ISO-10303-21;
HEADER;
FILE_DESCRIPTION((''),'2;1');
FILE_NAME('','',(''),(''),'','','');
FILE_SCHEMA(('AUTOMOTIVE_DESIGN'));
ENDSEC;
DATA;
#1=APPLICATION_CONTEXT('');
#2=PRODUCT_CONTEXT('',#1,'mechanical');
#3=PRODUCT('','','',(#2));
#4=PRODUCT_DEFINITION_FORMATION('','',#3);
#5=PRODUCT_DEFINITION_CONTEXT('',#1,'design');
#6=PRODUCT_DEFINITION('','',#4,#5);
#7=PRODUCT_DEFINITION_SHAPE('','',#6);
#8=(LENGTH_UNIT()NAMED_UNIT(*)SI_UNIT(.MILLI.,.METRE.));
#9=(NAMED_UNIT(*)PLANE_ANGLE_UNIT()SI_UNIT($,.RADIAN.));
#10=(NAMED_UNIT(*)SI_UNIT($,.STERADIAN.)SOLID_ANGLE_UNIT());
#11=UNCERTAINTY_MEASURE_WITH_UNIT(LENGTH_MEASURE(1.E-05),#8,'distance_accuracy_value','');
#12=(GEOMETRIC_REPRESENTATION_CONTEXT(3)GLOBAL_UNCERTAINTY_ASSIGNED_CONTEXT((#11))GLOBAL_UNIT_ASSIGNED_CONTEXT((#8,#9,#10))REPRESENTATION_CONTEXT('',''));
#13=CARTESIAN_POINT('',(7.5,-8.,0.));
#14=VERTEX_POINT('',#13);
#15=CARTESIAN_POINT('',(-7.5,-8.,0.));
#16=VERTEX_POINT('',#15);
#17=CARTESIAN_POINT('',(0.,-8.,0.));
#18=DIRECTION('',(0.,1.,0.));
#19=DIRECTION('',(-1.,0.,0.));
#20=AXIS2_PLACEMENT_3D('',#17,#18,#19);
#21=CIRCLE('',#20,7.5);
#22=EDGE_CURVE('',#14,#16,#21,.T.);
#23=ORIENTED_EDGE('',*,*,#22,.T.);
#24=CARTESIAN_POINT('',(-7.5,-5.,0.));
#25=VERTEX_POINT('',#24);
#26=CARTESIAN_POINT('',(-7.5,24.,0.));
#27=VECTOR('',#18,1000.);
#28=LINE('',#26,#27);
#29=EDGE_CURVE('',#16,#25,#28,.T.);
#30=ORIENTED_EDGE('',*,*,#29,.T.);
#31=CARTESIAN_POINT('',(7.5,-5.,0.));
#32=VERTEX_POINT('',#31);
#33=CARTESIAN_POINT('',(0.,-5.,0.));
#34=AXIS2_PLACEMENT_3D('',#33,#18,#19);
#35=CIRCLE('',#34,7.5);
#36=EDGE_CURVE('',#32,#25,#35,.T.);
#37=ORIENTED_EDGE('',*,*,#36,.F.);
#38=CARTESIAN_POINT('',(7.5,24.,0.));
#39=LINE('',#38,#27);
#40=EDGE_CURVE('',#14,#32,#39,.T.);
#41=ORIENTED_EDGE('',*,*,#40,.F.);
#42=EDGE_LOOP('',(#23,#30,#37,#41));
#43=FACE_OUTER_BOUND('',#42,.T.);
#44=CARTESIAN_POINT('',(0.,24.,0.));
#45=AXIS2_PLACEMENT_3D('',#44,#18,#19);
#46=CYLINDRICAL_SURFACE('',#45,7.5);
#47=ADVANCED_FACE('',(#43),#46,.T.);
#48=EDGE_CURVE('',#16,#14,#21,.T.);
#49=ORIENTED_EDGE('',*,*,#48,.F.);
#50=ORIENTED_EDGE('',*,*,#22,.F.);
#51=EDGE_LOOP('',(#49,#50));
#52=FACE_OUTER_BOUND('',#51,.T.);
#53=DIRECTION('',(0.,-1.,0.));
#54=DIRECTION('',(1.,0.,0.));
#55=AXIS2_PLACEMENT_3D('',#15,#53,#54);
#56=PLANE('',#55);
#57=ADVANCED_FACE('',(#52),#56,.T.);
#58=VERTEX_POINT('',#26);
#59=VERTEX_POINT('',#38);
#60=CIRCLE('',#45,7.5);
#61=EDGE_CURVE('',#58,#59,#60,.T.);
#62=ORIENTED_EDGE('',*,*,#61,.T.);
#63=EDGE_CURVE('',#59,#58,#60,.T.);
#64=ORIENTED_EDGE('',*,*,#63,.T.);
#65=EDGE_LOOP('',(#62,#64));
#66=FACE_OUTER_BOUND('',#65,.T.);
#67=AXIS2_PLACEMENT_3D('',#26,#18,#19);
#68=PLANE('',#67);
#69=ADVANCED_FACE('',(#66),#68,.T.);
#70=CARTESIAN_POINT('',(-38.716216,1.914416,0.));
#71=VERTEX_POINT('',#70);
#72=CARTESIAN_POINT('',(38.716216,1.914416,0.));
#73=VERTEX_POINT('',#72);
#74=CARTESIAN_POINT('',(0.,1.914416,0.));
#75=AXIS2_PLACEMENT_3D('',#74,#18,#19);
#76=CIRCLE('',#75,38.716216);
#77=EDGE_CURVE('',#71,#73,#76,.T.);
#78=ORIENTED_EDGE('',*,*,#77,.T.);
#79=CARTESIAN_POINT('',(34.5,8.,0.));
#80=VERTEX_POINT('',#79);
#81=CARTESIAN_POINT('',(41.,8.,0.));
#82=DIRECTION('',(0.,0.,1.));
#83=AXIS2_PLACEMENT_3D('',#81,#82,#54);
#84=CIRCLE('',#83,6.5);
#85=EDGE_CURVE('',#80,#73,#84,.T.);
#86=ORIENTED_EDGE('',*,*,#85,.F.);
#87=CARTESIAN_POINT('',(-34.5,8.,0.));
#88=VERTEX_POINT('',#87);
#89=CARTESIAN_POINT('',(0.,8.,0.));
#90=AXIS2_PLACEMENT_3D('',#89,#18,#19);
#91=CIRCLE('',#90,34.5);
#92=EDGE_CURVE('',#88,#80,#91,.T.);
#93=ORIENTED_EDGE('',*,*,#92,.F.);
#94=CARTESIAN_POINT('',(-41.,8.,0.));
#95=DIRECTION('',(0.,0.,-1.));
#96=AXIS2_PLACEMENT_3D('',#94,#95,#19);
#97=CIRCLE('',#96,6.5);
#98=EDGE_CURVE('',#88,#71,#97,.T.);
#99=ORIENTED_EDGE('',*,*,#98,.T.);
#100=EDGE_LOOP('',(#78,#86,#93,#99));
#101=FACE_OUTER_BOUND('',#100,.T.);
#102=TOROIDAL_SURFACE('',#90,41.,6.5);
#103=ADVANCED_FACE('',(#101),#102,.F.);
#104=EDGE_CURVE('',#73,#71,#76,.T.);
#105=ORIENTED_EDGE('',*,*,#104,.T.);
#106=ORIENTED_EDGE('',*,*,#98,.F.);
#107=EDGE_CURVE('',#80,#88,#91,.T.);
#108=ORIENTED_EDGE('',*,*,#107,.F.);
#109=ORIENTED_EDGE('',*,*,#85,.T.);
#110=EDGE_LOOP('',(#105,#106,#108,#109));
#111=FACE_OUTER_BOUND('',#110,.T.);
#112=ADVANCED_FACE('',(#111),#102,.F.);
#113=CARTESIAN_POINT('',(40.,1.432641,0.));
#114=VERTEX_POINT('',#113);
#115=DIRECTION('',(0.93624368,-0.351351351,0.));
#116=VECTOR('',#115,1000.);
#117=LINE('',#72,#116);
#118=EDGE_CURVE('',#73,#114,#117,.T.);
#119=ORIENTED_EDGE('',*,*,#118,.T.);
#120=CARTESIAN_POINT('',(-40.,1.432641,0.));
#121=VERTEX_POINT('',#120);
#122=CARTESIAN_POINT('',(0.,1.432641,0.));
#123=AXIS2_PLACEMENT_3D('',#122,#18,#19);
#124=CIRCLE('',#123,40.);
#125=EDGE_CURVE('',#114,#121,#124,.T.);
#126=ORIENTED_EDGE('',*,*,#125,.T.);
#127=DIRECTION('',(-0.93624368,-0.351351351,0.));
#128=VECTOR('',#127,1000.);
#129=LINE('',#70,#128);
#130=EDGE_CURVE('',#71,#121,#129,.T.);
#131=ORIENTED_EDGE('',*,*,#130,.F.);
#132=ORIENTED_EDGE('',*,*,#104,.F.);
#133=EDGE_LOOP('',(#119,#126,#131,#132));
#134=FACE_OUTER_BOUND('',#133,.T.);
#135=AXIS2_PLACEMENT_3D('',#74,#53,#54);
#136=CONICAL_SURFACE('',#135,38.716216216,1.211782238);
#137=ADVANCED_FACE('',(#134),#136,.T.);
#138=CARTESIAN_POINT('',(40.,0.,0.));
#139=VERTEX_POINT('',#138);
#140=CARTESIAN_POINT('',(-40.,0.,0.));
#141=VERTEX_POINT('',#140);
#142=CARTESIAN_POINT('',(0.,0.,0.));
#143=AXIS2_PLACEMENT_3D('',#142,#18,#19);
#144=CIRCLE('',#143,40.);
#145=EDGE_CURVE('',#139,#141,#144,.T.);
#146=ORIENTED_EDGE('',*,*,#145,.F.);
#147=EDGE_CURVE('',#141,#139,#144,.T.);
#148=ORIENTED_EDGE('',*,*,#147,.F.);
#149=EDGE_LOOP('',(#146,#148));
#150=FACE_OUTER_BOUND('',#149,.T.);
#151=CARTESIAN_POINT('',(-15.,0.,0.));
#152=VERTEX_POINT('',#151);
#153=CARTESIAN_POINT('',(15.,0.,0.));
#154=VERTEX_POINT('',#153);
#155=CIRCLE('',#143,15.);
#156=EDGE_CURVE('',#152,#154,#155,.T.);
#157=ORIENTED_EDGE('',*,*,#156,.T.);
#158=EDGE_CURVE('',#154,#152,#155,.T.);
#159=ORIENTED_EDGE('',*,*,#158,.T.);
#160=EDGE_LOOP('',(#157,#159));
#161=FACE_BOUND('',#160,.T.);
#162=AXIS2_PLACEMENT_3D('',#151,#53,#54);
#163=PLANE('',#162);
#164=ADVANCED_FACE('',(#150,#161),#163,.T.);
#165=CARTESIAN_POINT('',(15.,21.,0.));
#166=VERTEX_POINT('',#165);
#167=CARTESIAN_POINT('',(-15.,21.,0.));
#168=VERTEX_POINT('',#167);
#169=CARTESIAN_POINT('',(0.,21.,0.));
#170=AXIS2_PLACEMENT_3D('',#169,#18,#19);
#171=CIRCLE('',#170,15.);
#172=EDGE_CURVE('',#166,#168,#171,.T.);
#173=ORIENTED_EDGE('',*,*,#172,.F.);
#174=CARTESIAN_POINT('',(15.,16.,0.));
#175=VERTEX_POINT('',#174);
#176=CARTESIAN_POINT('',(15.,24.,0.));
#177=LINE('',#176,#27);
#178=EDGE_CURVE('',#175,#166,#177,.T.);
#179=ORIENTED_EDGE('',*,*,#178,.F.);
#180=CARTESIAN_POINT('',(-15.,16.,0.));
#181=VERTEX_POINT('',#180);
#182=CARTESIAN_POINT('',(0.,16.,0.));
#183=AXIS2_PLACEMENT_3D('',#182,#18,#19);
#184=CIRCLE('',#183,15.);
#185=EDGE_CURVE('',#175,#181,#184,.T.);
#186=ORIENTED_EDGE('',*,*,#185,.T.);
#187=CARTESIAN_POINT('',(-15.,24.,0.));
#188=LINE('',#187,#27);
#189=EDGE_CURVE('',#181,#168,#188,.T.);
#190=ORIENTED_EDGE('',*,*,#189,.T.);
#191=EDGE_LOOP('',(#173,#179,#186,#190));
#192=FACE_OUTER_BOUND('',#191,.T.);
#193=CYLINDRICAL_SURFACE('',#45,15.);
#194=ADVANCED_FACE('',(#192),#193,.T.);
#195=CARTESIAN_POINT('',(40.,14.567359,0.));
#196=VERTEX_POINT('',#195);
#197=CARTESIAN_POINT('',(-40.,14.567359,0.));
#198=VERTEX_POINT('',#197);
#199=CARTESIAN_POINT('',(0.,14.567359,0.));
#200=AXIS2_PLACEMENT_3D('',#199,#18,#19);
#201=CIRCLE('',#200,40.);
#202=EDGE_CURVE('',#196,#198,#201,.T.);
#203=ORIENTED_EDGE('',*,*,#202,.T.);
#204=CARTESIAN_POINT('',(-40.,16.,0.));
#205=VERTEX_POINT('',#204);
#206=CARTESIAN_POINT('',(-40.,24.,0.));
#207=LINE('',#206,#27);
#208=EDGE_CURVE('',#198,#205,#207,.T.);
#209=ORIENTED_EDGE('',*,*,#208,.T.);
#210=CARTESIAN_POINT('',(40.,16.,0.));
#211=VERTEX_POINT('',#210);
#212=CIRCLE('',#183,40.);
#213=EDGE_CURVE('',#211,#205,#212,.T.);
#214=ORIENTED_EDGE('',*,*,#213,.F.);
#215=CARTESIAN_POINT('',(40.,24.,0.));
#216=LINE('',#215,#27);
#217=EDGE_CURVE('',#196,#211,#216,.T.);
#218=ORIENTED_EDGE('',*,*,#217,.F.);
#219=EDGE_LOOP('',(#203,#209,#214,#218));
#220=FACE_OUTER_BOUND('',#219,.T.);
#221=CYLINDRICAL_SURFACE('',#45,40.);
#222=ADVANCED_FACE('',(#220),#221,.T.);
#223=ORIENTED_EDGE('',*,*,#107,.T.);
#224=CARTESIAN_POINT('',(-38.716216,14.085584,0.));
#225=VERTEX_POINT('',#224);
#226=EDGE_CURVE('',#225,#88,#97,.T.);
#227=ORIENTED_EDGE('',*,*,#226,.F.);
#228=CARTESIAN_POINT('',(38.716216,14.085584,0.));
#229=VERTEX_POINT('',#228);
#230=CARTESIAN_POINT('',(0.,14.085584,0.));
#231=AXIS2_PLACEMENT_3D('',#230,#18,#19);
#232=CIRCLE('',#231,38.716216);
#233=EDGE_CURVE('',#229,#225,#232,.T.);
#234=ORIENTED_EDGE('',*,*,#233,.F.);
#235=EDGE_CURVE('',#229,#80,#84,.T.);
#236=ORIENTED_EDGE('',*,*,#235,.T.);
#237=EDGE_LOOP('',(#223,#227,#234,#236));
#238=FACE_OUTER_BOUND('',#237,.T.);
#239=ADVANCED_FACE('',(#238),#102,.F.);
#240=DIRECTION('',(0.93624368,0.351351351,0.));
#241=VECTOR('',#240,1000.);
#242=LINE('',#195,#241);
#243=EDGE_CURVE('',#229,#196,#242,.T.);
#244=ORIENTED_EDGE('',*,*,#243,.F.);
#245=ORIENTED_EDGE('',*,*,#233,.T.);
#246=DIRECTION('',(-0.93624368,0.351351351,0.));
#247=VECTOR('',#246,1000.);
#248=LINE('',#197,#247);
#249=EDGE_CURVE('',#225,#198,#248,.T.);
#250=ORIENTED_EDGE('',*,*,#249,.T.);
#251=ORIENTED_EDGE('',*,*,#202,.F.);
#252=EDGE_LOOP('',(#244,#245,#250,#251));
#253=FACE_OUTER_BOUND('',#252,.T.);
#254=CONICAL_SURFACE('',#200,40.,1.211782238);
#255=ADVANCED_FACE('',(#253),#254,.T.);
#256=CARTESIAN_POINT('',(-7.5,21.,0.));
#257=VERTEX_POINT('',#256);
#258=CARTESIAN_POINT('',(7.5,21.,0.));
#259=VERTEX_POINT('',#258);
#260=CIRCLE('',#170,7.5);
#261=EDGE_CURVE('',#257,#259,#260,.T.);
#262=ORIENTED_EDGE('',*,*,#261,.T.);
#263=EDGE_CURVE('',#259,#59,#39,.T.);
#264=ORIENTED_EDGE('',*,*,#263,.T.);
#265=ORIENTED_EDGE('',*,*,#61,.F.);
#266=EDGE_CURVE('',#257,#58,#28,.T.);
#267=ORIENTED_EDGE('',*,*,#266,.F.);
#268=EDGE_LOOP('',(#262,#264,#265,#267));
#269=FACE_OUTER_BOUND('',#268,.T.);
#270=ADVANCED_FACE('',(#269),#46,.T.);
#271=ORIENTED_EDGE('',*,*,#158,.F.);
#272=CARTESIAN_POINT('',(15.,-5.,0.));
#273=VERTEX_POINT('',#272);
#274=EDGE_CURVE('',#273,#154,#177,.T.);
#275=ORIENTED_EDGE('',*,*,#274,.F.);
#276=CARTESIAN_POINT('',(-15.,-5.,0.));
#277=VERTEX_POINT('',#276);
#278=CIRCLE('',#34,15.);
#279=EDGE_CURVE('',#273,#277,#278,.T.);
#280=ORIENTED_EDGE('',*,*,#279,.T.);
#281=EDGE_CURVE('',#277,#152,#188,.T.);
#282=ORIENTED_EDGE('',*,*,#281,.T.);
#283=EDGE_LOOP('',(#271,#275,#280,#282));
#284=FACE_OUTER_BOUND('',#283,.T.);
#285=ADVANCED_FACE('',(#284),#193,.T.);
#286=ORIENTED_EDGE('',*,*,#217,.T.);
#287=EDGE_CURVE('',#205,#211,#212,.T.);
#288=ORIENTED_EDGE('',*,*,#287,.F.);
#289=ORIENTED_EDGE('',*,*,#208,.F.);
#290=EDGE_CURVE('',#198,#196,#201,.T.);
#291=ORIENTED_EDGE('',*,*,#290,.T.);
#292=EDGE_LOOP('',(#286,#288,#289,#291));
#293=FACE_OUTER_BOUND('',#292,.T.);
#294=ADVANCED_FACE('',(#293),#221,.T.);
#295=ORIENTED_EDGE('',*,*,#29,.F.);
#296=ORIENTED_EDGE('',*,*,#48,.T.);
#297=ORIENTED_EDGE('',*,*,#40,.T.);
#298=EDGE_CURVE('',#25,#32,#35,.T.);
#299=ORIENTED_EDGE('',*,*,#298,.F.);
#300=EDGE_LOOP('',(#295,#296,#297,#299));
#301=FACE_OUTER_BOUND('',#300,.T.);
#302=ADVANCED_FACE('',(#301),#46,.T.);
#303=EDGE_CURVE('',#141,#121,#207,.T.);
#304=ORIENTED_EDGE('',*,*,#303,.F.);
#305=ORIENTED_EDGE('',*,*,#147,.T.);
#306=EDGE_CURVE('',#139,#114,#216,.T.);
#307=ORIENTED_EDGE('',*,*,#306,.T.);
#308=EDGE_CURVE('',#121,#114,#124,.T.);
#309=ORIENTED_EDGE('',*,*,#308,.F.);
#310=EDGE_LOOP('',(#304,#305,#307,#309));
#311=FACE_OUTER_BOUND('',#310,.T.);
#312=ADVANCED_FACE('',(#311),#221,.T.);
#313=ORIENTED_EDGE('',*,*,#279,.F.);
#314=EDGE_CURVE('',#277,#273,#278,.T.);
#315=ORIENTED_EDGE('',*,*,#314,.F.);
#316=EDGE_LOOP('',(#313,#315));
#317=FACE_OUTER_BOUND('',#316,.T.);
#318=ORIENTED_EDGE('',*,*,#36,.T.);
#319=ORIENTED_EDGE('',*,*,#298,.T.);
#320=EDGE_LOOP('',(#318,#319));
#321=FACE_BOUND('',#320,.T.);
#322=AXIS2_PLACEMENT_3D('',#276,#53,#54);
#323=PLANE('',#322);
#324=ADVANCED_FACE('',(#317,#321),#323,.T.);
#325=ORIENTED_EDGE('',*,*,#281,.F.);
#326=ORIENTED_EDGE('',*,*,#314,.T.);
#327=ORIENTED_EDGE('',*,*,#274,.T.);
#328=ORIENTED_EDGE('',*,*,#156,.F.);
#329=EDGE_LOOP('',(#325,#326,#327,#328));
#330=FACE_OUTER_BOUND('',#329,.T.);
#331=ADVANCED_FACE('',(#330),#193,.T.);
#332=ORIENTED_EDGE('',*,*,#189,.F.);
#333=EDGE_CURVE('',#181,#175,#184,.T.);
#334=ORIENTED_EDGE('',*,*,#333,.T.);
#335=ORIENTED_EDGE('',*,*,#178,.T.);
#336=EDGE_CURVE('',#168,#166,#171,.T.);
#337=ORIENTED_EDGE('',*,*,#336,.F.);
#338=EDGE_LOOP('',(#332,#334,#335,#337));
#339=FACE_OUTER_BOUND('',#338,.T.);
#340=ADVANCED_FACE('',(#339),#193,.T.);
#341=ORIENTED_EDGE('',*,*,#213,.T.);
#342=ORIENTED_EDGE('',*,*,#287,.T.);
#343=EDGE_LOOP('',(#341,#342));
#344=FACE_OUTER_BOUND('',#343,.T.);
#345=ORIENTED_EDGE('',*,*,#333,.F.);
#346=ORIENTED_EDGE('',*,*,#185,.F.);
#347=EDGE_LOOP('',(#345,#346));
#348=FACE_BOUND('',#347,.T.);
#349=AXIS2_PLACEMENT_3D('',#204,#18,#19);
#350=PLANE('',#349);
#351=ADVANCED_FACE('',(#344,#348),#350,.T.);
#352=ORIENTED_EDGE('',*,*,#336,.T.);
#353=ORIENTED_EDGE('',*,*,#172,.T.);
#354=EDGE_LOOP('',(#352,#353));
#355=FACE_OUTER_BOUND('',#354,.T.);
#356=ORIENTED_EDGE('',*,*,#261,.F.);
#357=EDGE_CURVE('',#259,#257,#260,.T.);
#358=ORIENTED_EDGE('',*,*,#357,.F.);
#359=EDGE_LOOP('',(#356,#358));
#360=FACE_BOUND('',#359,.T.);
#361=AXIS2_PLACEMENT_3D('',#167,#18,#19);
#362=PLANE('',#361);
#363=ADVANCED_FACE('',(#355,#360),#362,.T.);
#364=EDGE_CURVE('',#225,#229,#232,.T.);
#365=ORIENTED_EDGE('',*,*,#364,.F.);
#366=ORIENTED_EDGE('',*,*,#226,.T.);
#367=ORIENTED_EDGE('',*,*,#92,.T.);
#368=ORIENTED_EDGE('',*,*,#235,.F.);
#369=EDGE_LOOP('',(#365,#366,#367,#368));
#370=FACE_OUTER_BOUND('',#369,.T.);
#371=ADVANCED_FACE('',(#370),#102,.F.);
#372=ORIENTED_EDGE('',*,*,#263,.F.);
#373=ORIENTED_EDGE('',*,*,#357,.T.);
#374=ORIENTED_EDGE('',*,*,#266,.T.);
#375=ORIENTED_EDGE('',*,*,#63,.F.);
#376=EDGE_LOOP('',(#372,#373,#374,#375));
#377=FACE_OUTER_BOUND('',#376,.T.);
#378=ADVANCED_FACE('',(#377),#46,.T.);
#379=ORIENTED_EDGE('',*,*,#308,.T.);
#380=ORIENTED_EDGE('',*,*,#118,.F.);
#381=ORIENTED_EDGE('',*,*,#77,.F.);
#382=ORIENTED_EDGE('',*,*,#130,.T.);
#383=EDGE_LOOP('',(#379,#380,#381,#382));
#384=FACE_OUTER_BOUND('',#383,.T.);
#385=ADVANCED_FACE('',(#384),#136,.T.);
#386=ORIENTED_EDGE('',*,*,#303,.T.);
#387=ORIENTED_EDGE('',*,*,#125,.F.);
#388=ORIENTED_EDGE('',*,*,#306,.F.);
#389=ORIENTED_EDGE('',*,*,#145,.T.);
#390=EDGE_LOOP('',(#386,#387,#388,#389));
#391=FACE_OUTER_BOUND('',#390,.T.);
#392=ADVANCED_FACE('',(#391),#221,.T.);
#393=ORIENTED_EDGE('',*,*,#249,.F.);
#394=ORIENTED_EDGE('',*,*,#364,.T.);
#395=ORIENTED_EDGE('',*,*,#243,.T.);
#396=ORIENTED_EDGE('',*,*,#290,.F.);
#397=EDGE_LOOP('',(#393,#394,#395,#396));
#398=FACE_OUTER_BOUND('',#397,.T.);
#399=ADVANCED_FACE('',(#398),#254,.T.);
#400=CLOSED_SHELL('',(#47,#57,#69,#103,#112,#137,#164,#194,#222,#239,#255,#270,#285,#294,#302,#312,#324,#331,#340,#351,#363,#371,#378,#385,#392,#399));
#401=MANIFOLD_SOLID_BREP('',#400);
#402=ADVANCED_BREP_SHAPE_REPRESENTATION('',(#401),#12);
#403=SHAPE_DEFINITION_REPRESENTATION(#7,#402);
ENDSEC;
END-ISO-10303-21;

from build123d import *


with BuildPart() as part:
    # Sketch1 → Revolve1 (revolve)
    with BuildSketch(Plane.XY):
        with BuildLine():
            Line((-15, 0), (-40, 0))
            Line((-40, 0), (-40, 1.432640688))
            Line((-40, 1.432640688), (-38.716216216, 1.914416082))
            ThreePointArc((-38.716216216, 1.914416082), (-34.5, 8), (-38.716216216, 14.085583918))
            Line((-38.716216216, 14.085583918), (-40, 14.567359312))
            Line((-40, 14.567359312), (-40, 16))
            Line((-40, 16), (-15, 16))
            Line((-15, 16), (-15, 21))
            Line((-15, 21), (-7.5, 21))
            Line((-7.5, 21), (-7.5, 24))
            Line((-7.5, 24), (0, 24))
            Line((0, 24), (0, -8))
            Line((0, -8), (-7.5, -8))
            Line((-7.5, -8), (-7.5, -5))
            Line((-7.5, -5), (-15, -5))
            Line((-15, -5), (-15, 0))
        make_face()
    revolve(axis=Axis((0, 24, 0), (0, -1, 0)))


solid = part.part
